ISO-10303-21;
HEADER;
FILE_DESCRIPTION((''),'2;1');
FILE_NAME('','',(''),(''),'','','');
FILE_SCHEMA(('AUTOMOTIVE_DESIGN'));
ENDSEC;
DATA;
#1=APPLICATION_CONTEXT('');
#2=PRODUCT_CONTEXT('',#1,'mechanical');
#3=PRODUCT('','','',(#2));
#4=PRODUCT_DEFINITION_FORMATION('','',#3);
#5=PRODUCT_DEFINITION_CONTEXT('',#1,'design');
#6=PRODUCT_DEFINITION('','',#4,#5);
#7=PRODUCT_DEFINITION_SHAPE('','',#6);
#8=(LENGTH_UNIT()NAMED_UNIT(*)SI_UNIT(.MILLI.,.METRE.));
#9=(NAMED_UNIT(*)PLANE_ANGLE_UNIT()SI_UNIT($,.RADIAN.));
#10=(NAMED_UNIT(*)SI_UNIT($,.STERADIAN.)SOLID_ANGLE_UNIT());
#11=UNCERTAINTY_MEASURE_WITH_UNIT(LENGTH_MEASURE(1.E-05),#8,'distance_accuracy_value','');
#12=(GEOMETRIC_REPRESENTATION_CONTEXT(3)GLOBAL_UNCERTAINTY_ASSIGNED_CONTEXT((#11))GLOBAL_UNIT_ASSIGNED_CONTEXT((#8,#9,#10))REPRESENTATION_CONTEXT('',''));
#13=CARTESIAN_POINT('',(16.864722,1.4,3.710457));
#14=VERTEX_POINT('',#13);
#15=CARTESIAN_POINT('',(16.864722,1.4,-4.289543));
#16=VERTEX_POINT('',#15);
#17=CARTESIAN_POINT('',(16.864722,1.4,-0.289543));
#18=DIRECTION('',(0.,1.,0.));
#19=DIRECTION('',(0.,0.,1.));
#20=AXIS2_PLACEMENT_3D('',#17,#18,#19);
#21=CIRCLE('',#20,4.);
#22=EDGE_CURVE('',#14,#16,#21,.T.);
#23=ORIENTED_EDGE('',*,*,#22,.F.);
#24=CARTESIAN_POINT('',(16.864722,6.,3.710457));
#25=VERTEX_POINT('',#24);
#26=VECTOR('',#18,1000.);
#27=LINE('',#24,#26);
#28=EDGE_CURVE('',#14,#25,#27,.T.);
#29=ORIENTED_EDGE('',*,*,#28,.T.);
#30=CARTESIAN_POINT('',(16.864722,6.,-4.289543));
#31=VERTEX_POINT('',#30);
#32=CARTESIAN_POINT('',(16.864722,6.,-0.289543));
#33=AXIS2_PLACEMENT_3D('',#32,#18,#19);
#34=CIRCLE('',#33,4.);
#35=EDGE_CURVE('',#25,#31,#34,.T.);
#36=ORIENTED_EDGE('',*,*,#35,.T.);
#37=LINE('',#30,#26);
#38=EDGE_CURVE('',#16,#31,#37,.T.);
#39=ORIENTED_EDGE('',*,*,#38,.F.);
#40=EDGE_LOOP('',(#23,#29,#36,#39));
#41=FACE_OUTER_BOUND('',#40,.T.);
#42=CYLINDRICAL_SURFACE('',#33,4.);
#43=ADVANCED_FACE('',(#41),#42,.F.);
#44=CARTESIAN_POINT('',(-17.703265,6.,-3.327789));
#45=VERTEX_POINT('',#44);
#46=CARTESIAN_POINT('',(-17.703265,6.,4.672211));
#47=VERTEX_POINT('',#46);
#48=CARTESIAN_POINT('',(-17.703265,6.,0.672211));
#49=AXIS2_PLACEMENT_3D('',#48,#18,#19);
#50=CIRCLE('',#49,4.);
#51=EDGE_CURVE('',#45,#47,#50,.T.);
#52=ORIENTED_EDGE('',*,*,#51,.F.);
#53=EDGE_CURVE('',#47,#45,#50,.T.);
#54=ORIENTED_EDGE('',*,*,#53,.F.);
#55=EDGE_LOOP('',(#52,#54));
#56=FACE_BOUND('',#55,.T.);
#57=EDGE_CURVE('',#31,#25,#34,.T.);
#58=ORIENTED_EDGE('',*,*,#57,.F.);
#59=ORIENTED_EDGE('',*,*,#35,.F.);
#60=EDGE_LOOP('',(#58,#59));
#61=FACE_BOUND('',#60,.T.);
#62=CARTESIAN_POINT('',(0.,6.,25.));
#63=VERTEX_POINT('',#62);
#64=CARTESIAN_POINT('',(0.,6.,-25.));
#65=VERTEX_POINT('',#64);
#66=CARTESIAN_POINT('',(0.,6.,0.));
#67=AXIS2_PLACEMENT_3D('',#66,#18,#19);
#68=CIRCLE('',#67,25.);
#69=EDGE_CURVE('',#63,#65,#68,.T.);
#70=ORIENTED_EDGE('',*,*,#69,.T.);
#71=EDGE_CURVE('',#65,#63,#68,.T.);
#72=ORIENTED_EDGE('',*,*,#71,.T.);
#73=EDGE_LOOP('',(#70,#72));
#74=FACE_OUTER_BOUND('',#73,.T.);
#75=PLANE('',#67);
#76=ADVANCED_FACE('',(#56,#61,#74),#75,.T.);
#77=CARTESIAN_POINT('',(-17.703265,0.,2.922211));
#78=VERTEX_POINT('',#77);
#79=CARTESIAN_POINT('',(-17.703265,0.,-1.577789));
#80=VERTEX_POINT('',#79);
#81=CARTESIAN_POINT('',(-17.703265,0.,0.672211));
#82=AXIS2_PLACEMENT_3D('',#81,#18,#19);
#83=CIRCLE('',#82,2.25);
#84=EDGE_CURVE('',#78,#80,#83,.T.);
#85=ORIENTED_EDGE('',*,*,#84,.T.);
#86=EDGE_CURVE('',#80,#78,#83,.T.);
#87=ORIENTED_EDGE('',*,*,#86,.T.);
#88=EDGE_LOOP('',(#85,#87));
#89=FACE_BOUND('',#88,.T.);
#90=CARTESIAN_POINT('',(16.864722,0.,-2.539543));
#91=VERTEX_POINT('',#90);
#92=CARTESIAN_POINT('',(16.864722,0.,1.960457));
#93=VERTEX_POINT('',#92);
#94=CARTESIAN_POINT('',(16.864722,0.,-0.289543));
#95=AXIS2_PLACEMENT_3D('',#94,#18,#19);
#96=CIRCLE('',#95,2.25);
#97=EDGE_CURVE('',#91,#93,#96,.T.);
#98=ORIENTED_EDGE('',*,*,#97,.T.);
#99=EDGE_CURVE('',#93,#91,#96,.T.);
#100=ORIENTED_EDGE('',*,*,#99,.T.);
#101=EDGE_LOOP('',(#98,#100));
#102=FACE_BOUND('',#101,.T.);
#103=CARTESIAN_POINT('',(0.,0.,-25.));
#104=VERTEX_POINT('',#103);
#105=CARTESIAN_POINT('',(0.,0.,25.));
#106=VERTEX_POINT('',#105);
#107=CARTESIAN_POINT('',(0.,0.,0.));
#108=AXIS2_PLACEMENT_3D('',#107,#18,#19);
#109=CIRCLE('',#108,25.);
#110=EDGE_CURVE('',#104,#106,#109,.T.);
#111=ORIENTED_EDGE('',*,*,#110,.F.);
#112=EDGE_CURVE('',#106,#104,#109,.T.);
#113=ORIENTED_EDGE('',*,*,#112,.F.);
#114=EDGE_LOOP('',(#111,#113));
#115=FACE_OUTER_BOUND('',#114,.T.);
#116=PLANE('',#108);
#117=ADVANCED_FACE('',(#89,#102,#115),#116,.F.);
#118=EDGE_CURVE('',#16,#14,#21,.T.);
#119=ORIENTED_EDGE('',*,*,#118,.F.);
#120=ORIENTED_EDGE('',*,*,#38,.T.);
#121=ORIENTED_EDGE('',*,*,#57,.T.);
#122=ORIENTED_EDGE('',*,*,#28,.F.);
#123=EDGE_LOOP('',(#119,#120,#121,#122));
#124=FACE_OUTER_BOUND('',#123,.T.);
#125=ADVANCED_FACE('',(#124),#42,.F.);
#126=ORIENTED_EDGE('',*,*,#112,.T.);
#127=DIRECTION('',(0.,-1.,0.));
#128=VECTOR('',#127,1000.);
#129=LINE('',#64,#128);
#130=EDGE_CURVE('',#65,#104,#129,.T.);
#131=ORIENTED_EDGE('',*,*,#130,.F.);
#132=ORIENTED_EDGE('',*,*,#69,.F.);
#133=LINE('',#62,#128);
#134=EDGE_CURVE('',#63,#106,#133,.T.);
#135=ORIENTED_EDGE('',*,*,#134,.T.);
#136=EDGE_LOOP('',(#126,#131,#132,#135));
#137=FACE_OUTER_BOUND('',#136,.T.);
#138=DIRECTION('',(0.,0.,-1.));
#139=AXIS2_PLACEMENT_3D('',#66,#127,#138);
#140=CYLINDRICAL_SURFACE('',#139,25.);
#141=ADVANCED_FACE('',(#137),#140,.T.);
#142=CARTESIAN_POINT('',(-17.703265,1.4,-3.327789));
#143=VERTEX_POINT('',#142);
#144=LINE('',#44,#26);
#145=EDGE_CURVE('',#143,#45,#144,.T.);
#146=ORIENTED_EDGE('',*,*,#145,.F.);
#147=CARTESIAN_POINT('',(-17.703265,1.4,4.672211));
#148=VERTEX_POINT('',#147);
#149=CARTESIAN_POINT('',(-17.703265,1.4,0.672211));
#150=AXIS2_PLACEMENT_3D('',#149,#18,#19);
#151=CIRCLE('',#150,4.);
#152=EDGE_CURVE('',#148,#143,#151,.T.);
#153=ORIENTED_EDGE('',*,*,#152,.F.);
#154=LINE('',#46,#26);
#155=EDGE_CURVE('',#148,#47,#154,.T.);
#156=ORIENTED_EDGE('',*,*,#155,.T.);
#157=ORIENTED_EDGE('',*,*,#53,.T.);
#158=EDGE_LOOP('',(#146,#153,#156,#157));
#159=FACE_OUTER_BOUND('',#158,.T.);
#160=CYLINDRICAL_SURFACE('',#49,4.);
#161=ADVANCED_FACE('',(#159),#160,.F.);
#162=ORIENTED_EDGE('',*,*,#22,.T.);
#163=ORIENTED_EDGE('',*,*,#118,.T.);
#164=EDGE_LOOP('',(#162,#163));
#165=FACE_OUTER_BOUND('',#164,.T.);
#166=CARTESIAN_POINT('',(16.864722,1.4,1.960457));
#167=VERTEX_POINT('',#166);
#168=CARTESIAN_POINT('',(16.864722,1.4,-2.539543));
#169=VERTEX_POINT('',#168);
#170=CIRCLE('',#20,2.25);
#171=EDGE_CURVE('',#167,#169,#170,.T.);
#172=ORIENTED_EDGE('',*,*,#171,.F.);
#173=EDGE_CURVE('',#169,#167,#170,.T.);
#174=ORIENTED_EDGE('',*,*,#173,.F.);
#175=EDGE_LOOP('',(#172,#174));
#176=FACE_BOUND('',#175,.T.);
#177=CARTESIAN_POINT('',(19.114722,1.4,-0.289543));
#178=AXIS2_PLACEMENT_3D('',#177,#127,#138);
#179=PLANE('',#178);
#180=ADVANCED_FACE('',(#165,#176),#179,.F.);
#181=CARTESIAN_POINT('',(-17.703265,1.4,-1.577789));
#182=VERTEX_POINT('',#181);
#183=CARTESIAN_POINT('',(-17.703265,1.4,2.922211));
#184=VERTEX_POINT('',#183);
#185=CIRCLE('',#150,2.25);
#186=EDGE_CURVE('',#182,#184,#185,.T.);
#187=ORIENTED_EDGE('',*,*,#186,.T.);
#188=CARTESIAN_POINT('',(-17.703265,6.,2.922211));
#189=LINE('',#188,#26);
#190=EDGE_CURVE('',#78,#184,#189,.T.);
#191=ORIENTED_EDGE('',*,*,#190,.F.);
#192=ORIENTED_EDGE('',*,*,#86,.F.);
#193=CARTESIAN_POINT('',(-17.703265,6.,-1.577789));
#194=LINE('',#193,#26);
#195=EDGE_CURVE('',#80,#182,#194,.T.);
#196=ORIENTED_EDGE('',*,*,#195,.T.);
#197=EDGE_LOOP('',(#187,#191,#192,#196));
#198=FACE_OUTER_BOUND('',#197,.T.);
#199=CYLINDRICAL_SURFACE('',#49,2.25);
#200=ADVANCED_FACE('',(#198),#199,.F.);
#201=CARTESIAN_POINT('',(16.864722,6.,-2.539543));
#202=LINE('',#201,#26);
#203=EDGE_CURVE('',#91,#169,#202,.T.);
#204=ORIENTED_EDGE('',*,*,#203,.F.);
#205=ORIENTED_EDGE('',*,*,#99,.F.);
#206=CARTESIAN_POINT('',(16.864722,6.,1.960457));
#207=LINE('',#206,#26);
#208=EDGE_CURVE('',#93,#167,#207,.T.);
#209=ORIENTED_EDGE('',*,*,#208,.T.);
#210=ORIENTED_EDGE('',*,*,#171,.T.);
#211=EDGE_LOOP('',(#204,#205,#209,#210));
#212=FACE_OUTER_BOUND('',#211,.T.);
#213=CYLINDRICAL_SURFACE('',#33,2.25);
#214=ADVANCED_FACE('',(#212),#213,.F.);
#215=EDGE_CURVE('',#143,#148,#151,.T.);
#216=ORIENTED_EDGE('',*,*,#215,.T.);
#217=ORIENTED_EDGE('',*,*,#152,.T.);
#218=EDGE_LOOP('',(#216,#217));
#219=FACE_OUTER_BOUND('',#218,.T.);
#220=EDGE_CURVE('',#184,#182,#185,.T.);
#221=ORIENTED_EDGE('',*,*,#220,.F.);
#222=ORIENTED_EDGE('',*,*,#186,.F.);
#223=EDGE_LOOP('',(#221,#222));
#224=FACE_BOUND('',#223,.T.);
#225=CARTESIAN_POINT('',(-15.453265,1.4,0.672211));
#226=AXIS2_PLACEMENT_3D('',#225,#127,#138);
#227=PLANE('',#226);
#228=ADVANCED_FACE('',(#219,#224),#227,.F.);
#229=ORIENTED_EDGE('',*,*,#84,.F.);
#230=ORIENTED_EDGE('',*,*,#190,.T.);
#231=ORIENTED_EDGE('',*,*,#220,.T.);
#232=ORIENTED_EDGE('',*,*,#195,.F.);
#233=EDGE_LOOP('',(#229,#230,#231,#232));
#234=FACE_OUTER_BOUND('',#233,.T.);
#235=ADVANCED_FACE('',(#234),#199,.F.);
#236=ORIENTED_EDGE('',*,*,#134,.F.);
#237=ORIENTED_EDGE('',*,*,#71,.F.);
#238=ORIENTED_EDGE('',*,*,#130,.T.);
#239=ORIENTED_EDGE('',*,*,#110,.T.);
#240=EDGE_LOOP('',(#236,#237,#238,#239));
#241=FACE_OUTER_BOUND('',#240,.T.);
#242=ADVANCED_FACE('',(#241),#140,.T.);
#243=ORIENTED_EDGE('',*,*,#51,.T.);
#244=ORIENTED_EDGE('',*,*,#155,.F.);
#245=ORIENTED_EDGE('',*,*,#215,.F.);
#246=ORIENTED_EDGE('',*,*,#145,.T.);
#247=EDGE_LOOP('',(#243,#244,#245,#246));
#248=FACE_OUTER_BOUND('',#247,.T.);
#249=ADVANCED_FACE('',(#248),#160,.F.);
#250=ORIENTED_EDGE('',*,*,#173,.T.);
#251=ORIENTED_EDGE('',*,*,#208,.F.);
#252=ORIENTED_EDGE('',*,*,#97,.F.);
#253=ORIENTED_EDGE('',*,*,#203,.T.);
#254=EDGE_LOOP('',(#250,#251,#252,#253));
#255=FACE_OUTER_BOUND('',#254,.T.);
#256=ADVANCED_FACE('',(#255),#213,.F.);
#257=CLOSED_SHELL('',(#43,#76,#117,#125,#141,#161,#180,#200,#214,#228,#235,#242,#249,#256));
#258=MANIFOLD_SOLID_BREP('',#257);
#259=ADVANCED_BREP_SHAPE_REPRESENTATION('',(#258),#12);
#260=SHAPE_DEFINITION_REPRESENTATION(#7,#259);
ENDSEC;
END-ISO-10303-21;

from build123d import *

# Parameters (mm, degrees)
SKETCH1_R                                            = 25
BOSS_EXTRUDE1_DEPTH                                  = 6
HOLE_SIZE_BASED_ON_SOCKET_HEAD_CAP_SCREW_D           = 4.5
HOLE_SIZE_BASED_ON_SOCKET_HEAD_CAP_SCREW_DEPTH       = 10.1
HOLE_SIZE_BASED_ON_SOCKET_HEAD_CAP_SCREW_CBORE_D     = 8
HOLE_SIZE_BASED_ON_SOCKET_HEAD_CAP_SCREW_CBORE_DEPTH = 4.6
HOLE_SIZE_BASED_ON_SOCKET_HEAD_CAP_SCREW_TIP         = 1.351936393


with BuildPart() as part:
    # Sketch1 → Boss-Extrude1 (new body)
    with BuildSketch(Plane(origin=(0, 0, 0), x_dir=(1, 0, 0), z_dir=(0, 1, 0))):
        with Locations(Location((0, 0, 0), (0, 0, 270))):
            Circle(SKETCH1_R)
    extrude(amount=BOSS_EXTRUDE1_DEPTH)

    # Hole size based on socket head cap screw type 1
    with Locations(Plane(origin=(16.864722122, 6, -0.289543132), x_dir=(0, 0, 1), z_dir=(0, 1, 0))):
        with Locations((0, 0), (0.961754182, -34.5679876)):
            CounterBoreHole(HOLE_SIZE_BASED_ON_SOCKET_HEAD_CAP_SCREW_D / 2, HOLE_SIZE_BASED_ON_SOCKET_HEAD_CAP_SCREW_CBORE_D / 2, HOLE_SIZE_BASED_ON_SOCKET_HEAD_CAP_SCREW_CBORE_DEPTH, depth=HOLE_SIZE_BASED_ON_SOCKET_HEAD_CAP_SCREW_DEPTH)
            with Locations((0, 0, -(HOLE_SIZE_BASED_ON_SOCKET_HEAD_CAP_SCREW_DEPTH + HOLE_SIZE_BASED_ON_SOCKET_HEAD_CAP_SCREW_TIP / 2))):  # 118° drill point
                Cone(0, HOLE_SIZE_BASED_ON_SOCKET_HEAD_CAP_SCREW_D / 2, HOLE_SIZE_BASED_ON_SOCKET_HEAD_CAP_SCREW_TIP, mode=Mode.SUBTRACT)


solid = part.part
